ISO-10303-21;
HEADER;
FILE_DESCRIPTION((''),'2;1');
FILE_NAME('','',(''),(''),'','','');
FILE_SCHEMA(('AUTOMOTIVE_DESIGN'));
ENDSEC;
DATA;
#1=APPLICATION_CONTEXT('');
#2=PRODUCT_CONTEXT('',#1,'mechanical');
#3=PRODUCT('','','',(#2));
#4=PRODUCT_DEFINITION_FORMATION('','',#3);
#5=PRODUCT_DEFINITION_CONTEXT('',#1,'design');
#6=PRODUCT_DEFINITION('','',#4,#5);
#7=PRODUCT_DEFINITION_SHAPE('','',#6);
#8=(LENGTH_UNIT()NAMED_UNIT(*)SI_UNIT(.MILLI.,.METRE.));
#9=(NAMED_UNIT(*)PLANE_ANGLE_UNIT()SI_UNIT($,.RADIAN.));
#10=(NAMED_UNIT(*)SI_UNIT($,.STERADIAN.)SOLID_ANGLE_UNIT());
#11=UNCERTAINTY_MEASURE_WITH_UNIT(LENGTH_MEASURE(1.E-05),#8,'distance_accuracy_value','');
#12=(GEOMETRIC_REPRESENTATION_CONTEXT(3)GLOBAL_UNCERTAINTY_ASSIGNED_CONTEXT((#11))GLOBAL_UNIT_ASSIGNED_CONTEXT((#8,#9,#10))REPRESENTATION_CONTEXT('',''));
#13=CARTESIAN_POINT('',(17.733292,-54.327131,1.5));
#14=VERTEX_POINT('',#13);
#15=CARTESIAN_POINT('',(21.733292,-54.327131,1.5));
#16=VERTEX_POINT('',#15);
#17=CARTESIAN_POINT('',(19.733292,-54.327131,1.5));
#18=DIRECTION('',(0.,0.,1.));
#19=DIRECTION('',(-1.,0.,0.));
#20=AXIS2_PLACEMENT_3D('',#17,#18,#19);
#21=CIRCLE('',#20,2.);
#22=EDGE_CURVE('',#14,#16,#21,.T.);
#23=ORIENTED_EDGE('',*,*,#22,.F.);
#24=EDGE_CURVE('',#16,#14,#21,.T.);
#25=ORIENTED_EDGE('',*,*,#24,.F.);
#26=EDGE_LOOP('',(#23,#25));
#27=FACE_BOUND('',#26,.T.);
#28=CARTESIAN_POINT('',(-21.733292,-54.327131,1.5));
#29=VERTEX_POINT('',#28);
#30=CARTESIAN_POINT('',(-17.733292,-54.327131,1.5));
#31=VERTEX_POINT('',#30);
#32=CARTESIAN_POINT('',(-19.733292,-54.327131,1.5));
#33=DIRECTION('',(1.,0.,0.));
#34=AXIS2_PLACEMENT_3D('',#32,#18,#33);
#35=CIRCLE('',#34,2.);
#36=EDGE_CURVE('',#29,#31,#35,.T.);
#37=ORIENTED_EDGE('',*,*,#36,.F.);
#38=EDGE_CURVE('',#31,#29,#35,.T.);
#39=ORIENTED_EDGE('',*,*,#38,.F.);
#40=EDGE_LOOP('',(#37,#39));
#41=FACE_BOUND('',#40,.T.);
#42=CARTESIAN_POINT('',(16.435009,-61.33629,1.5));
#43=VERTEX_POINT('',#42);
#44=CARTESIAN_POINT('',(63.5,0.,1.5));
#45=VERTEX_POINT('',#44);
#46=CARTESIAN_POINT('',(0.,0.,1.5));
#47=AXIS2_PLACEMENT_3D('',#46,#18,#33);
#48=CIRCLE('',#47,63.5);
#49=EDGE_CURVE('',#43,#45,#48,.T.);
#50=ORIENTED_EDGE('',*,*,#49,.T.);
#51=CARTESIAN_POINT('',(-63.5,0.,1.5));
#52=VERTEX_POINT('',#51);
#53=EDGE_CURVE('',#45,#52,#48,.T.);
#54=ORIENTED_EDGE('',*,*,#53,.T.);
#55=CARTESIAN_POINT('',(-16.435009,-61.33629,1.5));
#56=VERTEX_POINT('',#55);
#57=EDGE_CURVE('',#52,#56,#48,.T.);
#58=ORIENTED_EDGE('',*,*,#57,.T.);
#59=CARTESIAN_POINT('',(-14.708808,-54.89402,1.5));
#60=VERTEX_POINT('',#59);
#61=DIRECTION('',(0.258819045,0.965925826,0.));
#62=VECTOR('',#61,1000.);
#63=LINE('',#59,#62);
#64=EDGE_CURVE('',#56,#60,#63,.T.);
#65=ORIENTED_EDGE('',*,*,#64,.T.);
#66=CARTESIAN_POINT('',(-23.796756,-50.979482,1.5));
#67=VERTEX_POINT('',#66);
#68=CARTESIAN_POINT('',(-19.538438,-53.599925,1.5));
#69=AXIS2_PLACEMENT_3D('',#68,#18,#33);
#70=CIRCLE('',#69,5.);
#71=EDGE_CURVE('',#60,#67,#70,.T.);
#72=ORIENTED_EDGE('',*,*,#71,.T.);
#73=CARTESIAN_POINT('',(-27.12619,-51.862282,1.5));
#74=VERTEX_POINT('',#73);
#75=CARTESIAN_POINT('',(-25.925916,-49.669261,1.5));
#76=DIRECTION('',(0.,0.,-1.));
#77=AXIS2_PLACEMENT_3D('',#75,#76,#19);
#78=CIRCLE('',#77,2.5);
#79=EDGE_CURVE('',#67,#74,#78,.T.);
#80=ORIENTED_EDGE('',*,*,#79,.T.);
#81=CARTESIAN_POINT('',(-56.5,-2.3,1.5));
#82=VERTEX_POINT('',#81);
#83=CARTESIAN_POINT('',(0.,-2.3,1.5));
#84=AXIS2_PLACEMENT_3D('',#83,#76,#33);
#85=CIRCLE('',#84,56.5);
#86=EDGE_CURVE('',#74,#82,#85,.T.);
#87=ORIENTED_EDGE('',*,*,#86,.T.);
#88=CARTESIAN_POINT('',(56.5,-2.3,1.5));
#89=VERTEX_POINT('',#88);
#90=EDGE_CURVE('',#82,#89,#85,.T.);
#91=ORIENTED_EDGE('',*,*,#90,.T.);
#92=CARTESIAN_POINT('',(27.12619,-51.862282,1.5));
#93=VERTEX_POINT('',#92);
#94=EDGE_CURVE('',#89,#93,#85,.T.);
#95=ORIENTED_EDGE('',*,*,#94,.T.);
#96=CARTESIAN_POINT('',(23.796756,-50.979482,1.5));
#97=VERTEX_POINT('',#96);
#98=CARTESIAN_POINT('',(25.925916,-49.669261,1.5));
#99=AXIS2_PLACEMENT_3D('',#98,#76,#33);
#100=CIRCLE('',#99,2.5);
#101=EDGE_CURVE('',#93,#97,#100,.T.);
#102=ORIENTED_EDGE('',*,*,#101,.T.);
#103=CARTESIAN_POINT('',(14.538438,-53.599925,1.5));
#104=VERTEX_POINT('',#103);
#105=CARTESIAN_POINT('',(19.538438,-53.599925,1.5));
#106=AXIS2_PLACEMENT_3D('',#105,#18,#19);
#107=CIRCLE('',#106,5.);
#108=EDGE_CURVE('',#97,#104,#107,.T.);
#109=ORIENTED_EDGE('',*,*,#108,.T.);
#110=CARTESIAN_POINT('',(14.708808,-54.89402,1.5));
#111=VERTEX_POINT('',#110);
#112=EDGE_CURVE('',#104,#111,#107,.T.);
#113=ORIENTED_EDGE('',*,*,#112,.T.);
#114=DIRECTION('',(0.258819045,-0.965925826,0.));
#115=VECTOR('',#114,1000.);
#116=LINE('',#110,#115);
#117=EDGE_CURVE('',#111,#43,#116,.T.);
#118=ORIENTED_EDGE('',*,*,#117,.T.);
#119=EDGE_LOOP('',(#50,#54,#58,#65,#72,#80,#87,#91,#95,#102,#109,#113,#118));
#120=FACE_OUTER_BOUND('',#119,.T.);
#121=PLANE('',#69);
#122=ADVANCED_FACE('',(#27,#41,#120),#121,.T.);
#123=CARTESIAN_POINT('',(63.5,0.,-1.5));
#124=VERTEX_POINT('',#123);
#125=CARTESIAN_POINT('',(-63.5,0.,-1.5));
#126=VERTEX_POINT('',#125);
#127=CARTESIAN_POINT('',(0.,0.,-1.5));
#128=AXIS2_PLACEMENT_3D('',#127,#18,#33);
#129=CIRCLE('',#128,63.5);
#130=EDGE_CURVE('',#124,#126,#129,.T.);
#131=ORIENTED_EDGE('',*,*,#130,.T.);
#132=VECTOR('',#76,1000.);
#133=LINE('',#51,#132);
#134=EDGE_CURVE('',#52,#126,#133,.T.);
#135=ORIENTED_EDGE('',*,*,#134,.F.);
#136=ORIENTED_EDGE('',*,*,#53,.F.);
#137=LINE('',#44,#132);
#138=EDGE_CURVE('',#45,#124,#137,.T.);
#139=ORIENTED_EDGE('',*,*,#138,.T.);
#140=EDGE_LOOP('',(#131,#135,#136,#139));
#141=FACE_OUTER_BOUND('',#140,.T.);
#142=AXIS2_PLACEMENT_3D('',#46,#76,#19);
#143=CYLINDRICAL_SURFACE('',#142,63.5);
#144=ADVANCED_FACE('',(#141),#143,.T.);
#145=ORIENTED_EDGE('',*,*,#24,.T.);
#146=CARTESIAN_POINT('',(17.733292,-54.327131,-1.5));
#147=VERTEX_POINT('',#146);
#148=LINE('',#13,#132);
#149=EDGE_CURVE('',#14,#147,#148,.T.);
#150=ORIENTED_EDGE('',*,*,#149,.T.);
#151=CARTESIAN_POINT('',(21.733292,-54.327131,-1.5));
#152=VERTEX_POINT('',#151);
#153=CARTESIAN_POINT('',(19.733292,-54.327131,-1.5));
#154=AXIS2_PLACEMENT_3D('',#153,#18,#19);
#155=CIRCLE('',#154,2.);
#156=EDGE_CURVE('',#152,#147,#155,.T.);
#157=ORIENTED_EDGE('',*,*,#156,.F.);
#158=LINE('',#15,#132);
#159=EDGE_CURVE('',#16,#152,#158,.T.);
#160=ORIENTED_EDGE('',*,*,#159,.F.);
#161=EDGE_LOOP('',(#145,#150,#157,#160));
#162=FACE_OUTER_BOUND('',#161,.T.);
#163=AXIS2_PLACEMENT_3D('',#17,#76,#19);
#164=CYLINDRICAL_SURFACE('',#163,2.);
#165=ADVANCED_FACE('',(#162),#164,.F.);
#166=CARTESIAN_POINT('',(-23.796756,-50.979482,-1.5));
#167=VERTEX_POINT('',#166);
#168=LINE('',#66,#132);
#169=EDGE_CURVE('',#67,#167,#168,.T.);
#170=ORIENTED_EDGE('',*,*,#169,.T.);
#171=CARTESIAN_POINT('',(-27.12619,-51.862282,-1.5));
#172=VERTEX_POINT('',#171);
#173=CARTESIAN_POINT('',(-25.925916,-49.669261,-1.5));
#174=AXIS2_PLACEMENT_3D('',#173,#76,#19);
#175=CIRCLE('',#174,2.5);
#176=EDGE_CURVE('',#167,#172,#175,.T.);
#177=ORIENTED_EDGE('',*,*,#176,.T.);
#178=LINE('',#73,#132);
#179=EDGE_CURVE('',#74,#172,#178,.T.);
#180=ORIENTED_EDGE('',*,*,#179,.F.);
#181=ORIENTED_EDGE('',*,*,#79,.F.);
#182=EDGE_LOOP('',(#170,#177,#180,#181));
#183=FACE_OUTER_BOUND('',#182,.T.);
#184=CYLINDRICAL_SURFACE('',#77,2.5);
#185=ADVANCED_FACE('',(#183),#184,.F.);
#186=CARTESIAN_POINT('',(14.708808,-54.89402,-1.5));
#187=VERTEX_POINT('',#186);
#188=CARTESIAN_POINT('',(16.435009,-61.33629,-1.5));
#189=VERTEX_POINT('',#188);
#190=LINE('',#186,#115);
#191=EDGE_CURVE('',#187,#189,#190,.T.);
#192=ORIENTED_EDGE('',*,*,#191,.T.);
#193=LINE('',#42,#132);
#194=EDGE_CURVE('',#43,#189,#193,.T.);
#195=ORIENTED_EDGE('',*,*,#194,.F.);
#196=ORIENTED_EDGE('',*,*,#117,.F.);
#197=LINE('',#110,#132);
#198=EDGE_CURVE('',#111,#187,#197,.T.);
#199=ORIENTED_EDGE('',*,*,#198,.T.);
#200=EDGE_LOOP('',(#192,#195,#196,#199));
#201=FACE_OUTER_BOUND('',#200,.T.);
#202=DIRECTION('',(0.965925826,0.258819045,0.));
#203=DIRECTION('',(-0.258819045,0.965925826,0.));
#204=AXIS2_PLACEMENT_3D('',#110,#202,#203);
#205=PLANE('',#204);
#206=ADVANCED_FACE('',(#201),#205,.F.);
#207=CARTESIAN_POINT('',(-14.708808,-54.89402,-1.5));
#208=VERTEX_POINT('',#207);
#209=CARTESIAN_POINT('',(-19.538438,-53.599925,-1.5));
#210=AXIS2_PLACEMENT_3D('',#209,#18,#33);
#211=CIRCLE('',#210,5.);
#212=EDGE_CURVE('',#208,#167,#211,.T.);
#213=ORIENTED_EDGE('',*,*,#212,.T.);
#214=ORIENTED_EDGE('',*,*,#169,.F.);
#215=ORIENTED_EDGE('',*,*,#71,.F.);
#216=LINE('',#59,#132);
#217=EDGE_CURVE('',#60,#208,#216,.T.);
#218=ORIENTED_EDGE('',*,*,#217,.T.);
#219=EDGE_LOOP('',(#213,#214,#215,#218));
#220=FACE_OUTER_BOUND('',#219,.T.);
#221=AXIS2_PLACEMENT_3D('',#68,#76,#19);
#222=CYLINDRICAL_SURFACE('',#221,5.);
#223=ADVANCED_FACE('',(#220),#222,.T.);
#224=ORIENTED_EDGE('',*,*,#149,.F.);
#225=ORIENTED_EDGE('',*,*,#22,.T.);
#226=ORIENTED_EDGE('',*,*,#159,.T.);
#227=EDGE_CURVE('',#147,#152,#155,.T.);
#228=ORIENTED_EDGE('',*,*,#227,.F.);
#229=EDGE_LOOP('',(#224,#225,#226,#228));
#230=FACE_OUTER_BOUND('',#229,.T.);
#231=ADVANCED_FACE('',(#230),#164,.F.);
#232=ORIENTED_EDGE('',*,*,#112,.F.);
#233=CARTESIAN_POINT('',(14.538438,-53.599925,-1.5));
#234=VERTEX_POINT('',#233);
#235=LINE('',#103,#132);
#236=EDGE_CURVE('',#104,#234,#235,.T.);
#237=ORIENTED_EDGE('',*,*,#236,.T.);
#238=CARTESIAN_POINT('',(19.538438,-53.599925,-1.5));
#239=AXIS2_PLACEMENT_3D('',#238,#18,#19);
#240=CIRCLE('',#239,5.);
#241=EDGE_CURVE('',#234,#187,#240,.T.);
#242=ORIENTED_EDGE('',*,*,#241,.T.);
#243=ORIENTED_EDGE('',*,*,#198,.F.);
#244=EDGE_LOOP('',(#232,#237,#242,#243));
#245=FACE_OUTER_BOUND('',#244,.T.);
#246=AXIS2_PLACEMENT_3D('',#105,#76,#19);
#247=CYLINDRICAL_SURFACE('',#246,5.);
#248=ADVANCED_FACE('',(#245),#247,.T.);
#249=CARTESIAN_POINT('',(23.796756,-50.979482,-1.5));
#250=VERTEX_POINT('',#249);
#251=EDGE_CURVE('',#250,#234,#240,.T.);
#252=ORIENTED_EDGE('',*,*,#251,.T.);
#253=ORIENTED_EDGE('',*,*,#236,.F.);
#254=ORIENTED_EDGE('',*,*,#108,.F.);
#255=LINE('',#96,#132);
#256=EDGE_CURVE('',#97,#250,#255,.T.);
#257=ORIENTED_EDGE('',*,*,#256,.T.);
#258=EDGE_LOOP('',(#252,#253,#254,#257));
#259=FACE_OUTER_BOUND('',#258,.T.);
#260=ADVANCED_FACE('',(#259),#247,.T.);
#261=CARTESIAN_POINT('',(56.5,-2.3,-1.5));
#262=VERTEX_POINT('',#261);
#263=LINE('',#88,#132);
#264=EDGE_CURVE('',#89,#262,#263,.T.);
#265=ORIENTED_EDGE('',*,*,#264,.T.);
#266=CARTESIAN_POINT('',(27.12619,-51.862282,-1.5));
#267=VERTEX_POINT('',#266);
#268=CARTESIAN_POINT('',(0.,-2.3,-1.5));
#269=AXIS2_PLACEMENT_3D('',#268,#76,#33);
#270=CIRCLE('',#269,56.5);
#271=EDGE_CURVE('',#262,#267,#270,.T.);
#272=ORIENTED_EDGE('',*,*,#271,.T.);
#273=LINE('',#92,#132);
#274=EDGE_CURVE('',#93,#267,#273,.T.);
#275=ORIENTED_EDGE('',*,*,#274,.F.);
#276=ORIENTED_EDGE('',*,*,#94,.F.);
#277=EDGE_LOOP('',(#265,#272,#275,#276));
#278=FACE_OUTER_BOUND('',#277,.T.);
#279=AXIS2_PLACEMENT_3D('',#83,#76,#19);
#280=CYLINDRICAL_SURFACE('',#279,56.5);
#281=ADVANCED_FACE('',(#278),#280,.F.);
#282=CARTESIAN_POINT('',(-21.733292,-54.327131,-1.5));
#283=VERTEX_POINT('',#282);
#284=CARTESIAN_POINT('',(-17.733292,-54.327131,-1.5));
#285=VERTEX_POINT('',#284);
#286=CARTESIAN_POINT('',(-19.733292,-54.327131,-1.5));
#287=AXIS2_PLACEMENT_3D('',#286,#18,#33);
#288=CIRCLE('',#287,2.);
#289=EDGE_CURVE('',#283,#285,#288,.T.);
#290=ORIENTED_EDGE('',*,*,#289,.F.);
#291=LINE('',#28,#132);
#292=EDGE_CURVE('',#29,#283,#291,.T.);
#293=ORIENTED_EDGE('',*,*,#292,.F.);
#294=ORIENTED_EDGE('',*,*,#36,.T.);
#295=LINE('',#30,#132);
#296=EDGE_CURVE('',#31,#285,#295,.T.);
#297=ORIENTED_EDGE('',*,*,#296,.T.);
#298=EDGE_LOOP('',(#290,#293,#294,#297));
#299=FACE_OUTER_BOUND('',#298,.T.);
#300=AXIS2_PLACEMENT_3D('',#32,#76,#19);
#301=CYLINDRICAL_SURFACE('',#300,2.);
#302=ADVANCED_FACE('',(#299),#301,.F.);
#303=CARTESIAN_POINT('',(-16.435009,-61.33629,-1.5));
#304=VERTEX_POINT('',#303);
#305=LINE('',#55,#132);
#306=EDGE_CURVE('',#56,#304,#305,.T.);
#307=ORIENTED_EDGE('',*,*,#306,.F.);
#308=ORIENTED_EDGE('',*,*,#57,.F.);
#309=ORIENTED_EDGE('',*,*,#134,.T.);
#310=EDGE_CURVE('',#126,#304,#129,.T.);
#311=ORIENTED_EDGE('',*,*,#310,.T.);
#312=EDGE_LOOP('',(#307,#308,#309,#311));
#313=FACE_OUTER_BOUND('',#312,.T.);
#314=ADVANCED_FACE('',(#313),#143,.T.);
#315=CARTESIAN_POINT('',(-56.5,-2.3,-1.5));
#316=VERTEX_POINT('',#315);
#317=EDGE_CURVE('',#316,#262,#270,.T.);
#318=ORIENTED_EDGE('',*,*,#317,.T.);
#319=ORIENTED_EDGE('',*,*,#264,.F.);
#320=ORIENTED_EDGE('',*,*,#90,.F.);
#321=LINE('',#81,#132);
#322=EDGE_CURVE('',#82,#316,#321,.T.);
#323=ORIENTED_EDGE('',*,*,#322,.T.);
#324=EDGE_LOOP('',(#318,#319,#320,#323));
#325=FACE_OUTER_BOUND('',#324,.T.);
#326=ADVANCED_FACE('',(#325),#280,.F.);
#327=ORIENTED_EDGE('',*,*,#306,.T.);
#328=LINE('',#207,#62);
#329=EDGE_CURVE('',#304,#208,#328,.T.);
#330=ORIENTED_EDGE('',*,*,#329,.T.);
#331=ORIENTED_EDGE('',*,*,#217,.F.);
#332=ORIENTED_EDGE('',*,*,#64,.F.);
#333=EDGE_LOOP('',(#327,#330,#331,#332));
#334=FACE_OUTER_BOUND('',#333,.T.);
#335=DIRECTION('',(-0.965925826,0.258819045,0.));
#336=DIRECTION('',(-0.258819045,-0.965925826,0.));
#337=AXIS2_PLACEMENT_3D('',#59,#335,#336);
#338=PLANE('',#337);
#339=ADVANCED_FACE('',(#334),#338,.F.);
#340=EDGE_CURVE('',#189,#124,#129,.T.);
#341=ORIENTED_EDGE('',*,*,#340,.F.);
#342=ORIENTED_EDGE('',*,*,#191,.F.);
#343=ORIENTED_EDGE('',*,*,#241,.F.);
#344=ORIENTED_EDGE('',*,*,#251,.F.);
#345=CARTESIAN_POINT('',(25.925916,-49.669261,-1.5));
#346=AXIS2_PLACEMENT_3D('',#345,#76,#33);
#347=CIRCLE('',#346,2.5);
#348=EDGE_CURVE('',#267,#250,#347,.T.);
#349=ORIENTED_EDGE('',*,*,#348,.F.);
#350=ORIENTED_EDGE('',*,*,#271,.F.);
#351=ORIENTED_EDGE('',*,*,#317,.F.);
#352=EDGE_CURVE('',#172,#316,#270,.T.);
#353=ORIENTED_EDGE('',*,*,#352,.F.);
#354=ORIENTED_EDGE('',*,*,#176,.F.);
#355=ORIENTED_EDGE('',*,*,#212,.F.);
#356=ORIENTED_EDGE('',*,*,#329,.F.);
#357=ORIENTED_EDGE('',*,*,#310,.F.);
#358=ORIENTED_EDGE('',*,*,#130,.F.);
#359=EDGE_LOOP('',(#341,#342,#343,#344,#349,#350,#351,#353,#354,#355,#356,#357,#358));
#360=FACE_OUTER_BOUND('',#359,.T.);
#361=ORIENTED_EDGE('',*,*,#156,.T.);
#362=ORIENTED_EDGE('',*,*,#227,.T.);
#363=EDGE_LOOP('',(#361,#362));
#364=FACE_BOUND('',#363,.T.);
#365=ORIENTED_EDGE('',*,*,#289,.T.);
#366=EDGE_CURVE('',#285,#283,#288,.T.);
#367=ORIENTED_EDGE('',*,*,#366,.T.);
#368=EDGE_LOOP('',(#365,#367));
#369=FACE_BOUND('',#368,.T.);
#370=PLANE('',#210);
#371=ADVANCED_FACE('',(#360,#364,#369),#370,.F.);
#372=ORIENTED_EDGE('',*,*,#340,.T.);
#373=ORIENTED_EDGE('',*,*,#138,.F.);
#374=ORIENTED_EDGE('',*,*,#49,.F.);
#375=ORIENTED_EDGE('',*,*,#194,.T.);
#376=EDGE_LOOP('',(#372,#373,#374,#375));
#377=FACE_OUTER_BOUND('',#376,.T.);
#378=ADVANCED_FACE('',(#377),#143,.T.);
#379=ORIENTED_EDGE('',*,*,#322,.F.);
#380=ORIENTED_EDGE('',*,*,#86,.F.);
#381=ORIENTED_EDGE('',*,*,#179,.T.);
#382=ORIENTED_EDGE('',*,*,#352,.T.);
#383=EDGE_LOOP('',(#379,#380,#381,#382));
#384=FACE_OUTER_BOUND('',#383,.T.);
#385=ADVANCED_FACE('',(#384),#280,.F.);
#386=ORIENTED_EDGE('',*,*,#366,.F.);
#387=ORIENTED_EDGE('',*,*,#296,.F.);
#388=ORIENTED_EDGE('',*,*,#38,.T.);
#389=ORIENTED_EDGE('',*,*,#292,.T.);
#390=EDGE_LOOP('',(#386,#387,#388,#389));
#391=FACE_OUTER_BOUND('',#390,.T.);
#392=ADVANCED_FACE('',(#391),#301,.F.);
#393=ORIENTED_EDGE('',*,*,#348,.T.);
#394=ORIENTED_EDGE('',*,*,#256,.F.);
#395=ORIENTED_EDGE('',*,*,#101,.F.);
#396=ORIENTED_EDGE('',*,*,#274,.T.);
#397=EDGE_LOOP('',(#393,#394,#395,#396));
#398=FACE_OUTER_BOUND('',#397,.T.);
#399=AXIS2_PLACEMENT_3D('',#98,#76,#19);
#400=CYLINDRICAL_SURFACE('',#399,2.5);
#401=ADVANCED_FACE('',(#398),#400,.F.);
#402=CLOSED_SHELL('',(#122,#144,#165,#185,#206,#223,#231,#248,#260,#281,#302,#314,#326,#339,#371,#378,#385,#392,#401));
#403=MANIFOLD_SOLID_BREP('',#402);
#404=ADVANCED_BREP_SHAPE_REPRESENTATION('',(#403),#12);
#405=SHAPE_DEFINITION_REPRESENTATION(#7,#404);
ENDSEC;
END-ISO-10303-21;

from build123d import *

# Parameters (mm, degrees)
BASE_EXTRUDE_DEPTH      = 1.5
BASE_EXTRUDE_DEPTH_BACK = 1.5
SKETCH1_R               = 2


with BuildPart() as part:
    # Sketch1 → Base-Extrude (new, two sides: drawn at the far end of the back side and taken through both)
    with BuildSketch(Plane.XY.offset(-BASE_EXTRUDE_DEPTH_BACK)):
        with BuildLine():
            Line((-14.708808387, -54.894020219), (-16.435009364, -61.336289969))
            ThreePointArc((-16.435009364, -61.336289969), (0, 63.5), (16.435009364, -61.336289969))
            Line((16.435009364, -61.336289969), (14.708808387, -54.894020219))
            ThreePointArc((14.708808387, -54.894020219), (17.560433321, -49.007812256), (23.796756449, -50.979482305))
            ThreePointArc((23.796756449, -50.979482305), (25.28518113, -52.085758206), (27.1261898, -51.862282302))
            ThreePointArc((27.1261898, -51.862282302), (0, 54.2), (-27.1261898, -51.862282302))
            ThreePointArc((-27.1261898, -51.862282302), (-25.28518113, -52.085758206), (-23.796756449, -50.979482305))
            ThreePointArc((-23.796756449, -50.979482305), (-17.560433321, -49.007812256), (-14.708808387, -54.894020219))
        make_face()
        with Locations((-19.733291854, -54.327131275)):
            Circle(SKETCH1_R, mode=Mode.SUBTRACT)
        with Locations(Location((19.733291854, -54.327131275, 0), (0, 0, 180))):
            Circle(SKETCH1_R, mode=Mode.SUBTRACT)
    extrude(amount=BASE_EXTRUDE_DEPTH + BASE_EXTRUDE_DEPTH_BACK)


solid = part.part
